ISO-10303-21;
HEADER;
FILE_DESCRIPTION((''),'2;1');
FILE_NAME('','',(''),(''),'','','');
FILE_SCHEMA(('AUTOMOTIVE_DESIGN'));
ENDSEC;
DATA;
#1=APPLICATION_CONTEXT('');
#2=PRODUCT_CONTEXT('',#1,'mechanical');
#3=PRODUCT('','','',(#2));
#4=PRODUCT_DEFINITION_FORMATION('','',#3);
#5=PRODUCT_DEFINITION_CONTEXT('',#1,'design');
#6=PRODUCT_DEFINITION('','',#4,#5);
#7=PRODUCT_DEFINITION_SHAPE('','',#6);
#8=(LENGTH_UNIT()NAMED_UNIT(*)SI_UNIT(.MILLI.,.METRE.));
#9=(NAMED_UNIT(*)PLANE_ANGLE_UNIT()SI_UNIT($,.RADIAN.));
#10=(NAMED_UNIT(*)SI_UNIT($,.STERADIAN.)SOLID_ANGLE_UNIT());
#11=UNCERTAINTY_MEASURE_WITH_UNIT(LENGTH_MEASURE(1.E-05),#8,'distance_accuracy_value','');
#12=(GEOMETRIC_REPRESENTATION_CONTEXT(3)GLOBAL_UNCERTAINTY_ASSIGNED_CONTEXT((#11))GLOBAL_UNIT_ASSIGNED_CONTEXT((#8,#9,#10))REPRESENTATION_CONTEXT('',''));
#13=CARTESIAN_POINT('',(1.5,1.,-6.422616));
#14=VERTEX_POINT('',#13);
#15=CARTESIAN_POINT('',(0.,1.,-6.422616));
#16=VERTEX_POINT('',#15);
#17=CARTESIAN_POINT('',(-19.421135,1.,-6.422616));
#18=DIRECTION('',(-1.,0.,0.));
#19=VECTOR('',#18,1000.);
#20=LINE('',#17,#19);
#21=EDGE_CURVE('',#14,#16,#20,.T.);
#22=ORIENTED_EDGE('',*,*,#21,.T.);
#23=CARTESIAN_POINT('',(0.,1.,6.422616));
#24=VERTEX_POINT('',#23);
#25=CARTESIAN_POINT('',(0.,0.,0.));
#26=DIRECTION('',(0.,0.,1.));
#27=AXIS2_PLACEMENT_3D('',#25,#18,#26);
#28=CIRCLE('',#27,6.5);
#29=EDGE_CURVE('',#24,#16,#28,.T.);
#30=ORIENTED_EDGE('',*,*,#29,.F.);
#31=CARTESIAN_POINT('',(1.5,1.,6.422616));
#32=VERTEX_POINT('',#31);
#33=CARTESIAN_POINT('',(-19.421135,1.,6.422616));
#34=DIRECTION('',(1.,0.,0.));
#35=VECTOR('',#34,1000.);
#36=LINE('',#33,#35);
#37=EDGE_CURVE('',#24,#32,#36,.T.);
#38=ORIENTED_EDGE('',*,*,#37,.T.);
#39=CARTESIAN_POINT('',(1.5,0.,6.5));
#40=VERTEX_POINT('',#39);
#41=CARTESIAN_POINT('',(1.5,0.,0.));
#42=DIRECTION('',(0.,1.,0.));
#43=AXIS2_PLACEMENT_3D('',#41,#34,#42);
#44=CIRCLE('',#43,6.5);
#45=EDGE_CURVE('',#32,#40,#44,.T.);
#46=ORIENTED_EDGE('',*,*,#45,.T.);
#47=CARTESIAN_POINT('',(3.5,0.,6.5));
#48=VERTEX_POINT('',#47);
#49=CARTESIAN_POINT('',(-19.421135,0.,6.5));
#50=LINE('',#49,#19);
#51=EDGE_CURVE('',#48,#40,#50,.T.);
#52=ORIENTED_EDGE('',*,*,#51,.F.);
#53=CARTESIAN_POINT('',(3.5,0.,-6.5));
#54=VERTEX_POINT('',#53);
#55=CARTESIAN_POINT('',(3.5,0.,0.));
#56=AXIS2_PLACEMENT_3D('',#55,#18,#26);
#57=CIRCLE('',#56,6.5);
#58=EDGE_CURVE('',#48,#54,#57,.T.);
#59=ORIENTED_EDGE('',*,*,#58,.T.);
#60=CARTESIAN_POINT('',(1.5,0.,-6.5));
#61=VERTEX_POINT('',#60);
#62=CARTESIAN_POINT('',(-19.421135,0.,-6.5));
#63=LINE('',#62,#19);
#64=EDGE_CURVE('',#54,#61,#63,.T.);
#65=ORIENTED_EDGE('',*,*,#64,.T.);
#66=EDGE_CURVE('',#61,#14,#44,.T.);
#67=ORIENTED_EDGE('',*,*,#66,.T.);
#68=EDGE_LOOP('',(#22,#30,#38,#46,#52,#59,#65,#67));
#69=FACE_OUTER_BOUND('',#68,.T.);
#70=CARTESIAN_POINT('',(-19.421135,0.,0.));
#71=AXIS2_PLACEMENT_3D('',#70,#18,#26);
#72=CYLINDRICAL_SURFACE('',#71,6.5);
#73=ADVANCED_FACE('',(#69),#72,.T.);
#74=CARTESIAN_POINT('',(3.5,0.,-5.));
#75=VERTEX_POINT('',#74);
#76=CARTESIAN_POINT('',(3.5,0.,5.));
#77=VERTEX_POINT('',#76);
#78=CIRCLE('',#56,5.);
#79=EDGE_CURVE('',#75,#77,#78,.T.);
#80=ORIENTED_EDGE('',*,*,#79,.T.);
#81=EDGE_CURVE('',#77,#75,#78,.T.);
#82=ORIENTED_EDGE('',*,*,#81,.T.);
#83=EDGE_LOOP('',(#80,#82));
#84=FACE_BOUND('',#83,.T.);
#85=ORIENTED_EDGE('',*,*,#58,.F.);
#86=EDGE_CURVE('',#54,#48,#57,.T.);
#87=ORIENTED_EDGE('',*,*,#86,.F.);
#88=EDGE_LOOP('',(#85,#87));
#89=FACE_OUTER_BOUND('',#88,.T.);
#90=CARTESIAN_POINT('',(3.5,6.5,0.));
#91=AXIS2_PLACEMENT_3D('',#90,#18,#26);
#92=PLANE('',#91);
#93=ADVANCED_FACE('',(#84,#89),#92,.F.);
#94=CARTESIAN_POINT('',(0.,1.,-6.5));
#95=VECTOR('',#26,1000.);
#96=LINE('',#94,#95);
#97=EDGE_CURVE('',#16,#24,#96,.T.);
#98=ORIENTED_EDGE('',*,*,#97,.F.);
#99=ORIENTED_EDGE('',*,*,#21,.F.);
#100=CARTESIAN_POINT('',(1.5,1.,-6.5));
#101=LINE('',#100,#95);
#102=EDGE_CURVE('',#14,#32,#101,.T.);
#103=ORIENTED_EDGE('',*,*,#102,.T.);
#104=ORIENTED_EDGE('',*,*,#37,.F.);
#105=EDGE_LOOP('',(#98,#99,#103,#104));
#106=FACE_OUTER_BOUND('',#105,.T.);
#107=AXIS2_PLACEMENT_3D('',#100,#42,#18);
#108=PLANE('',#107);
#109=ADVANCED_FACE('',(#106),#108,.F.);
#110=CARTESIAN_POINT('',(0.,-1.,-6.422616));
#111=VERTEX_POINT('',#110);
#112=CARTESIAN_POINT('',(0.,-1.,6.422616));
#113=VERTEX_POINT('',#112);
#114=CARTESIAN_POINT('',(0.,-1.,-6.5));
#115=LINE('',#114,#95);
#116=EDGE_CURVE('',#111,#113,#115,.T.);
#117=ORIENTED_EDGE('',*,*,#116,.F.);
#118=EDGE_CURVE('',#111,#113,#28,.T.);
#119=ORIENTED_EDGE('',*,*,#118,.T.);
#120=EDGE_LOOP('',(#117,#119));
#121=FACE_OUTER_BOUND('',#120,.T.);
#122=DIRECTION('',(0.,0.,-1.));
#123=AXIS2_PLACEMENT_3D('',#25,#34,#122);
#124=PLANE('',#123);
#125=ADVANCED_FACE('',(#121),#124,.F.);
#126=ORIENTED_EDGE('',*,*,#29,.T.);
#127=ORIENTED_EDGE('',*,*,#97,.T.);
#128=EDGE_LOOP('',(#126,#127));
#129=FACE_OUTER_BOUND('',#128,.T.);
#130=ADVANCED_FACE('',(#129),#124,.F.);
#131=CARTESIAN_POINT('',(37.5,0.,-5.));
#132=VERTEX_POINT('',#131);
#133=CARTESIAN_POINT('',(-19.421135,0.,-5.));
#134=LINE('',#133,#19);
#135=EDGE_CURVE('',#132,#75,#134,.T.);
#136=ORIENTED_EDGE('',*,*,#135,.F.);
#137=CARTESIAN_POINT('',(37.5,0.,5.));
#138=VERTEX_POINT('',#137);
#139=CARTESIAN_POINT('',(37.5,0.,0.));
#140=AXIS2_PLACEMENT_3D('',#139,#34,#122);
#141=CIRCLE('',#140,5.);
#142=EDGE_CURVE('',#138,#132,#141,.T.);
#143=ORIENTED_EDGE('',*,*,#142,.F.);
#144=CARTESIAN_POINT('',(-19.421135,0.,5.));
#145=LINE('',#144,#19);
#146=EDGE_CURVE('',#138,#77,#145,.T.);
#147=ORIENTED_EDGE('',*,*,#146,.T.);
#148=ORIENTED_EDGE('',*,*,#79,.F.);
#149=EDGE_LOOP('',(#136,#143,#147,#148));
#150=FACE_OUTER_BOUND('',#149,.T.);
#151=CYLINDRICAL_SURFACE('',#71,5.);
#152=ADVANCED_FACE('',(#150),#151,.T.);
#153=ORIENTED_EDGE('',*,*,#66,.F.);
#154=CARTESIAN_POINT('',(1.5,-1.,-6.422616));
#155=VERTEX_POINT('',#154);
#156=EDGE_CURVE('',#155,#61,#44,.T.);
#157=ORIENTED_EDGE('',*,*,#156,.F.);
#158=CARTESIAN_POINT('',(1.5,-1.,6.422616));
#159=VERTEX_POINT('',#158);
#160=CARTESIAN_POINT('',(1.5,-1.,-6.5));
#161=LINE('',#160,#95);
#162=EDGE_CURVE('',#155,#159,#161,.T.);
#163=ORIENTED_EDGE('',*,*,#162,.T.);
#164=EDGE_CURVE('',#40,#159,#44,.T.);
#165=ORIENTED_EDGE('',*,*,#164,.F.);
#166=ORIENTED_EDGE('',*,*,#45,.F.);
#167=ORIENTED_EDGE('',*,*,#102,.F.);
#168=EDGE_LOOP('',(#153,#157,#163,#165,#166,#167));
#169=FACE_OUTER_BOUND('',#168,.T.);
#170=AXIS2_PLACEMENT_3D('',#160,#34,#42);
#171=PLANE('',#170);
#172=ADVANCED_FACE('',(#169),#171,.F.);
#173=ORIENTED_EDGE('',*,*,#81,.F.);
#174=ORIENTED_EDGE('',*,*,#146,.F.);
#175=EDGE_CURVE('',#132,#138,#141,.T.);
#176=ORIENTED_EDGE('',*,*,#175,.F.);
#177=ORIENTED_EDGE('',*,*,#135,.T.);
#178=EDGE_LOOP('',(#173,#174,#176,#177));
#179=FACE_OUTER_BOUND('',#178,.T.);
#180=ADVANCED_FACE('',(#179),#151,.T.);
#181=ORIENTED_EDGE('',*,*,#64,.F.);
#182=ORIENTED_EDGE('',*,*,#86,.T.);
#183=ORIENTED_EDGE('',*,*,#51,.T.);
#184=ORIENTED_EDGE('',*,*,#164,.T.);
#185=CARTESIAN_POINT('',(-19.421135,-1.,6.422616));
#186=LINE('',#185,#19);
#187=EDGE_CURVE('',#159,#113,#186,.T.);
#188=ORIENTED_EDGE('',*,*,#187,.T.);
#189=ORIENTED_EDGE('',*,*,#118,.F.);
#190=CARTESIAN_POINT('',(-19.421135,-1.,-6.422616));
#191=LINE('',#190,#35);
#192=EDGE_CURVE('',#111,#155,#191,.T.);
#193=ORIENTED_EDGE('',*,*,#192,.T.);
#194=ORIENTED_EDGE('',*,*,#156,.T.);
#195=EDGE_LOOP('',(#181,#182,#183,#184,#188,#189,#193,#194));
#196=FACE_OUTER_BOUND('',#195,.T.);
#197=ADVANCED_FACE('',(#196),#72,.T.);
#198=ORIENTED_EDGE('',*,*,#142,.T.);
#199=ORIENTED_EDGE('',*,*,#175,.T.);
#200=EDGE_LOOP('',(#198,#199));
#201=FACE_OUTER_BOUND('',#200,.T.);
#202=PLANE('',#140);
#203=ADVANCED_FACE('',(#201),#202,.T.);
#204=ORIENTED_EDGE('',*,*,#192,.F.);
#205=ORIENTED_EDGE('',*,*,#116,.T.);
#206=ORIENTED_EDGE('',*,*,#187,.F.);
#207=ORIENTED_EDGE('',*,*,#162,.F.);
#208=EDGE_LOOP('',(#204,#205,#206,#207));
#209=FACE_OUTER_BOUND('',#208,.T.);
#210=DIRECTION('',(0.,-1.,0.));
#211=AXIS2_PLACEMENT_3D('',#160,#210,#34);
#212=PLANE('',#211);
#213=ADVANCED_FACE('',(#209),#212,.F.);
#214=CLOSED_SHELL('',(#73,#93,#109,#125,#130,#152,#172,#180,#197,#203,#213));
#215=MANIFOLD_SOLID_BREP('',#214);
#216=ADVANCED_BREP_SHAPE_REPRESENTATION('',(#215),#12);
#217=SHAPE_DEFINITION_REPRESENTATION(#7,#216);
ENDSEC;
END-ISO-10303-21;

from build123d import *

# Parameters (mm, degrees)
CHAMFER_2_SIZE           = 1
CUT_EXTRUDE_1_DEPTH      = 49.38129804
CUT_EXTRUDE_1_DEPTH_BACK = 49.38129804
SKETCH_2_W               = 1.5
SKETCH_2_H               = 2
SKETCH_3_R               = 5.5
CUT_EXTRUDE_2_DEPTH      = 10


with BuildPart() as part:
    # 草图1 → 旋转1 (revolve)
    with BuildSketch(Plane.XY, mode=Mode.PRIVATE) as revolve_1_sk:
        Polygon((0, 0), (0, 6.5), (3.5, 6.5), (3.5, 5), (47.5, 5), (47.5, 0), align=None)
    revolve(revolve_1_sk.sketch.rotate(Axis((-19.421134541, 0, 0), (1, 0, 0)), 90), axis=Axis((-19.421134541, 0, 0), (1, 0, 0)))

    # 倒角2
    chamfer_2_edges = [part.edges().sort_by_distance(p)[0] for p in [
        (47.5, 0, -5),
    ]]
    chamfer(chamfer_2_edges, length=CHAMFER_2_SIZE)

    # 草图2 → 切除-拉伸1 (cut, two sides: drawn at the far end of the back side and taken through both)
    with BuildSketch(Plane.XY.offset(-CUT_EXTRUDE_1_DEPTH_BACK)):
        with Locations((0.75, 0)):
            Rectangle(SKETCH_2_W, SKETCH_2_H)
    extrude(amount=CUT_EXTRUDE_1_DEPTH + CUT_EXTRUDE_1_DEPTH_BACK, mode=Mode.SUBTRACT)

    # 草图3 → 切除-拉伸2 (cut)
    with BuildSketch(Plane(origin=(47.5, 0, 0), x_dir=(0, 0, -1), z_dir=(1, 0, 0))):
        Circle(SKETCH_3_R)
    extrude(amount=-CUT_EXTRUDE_2_DEPTH, mode=Mode.SUBTRACT)


solid = part.part
